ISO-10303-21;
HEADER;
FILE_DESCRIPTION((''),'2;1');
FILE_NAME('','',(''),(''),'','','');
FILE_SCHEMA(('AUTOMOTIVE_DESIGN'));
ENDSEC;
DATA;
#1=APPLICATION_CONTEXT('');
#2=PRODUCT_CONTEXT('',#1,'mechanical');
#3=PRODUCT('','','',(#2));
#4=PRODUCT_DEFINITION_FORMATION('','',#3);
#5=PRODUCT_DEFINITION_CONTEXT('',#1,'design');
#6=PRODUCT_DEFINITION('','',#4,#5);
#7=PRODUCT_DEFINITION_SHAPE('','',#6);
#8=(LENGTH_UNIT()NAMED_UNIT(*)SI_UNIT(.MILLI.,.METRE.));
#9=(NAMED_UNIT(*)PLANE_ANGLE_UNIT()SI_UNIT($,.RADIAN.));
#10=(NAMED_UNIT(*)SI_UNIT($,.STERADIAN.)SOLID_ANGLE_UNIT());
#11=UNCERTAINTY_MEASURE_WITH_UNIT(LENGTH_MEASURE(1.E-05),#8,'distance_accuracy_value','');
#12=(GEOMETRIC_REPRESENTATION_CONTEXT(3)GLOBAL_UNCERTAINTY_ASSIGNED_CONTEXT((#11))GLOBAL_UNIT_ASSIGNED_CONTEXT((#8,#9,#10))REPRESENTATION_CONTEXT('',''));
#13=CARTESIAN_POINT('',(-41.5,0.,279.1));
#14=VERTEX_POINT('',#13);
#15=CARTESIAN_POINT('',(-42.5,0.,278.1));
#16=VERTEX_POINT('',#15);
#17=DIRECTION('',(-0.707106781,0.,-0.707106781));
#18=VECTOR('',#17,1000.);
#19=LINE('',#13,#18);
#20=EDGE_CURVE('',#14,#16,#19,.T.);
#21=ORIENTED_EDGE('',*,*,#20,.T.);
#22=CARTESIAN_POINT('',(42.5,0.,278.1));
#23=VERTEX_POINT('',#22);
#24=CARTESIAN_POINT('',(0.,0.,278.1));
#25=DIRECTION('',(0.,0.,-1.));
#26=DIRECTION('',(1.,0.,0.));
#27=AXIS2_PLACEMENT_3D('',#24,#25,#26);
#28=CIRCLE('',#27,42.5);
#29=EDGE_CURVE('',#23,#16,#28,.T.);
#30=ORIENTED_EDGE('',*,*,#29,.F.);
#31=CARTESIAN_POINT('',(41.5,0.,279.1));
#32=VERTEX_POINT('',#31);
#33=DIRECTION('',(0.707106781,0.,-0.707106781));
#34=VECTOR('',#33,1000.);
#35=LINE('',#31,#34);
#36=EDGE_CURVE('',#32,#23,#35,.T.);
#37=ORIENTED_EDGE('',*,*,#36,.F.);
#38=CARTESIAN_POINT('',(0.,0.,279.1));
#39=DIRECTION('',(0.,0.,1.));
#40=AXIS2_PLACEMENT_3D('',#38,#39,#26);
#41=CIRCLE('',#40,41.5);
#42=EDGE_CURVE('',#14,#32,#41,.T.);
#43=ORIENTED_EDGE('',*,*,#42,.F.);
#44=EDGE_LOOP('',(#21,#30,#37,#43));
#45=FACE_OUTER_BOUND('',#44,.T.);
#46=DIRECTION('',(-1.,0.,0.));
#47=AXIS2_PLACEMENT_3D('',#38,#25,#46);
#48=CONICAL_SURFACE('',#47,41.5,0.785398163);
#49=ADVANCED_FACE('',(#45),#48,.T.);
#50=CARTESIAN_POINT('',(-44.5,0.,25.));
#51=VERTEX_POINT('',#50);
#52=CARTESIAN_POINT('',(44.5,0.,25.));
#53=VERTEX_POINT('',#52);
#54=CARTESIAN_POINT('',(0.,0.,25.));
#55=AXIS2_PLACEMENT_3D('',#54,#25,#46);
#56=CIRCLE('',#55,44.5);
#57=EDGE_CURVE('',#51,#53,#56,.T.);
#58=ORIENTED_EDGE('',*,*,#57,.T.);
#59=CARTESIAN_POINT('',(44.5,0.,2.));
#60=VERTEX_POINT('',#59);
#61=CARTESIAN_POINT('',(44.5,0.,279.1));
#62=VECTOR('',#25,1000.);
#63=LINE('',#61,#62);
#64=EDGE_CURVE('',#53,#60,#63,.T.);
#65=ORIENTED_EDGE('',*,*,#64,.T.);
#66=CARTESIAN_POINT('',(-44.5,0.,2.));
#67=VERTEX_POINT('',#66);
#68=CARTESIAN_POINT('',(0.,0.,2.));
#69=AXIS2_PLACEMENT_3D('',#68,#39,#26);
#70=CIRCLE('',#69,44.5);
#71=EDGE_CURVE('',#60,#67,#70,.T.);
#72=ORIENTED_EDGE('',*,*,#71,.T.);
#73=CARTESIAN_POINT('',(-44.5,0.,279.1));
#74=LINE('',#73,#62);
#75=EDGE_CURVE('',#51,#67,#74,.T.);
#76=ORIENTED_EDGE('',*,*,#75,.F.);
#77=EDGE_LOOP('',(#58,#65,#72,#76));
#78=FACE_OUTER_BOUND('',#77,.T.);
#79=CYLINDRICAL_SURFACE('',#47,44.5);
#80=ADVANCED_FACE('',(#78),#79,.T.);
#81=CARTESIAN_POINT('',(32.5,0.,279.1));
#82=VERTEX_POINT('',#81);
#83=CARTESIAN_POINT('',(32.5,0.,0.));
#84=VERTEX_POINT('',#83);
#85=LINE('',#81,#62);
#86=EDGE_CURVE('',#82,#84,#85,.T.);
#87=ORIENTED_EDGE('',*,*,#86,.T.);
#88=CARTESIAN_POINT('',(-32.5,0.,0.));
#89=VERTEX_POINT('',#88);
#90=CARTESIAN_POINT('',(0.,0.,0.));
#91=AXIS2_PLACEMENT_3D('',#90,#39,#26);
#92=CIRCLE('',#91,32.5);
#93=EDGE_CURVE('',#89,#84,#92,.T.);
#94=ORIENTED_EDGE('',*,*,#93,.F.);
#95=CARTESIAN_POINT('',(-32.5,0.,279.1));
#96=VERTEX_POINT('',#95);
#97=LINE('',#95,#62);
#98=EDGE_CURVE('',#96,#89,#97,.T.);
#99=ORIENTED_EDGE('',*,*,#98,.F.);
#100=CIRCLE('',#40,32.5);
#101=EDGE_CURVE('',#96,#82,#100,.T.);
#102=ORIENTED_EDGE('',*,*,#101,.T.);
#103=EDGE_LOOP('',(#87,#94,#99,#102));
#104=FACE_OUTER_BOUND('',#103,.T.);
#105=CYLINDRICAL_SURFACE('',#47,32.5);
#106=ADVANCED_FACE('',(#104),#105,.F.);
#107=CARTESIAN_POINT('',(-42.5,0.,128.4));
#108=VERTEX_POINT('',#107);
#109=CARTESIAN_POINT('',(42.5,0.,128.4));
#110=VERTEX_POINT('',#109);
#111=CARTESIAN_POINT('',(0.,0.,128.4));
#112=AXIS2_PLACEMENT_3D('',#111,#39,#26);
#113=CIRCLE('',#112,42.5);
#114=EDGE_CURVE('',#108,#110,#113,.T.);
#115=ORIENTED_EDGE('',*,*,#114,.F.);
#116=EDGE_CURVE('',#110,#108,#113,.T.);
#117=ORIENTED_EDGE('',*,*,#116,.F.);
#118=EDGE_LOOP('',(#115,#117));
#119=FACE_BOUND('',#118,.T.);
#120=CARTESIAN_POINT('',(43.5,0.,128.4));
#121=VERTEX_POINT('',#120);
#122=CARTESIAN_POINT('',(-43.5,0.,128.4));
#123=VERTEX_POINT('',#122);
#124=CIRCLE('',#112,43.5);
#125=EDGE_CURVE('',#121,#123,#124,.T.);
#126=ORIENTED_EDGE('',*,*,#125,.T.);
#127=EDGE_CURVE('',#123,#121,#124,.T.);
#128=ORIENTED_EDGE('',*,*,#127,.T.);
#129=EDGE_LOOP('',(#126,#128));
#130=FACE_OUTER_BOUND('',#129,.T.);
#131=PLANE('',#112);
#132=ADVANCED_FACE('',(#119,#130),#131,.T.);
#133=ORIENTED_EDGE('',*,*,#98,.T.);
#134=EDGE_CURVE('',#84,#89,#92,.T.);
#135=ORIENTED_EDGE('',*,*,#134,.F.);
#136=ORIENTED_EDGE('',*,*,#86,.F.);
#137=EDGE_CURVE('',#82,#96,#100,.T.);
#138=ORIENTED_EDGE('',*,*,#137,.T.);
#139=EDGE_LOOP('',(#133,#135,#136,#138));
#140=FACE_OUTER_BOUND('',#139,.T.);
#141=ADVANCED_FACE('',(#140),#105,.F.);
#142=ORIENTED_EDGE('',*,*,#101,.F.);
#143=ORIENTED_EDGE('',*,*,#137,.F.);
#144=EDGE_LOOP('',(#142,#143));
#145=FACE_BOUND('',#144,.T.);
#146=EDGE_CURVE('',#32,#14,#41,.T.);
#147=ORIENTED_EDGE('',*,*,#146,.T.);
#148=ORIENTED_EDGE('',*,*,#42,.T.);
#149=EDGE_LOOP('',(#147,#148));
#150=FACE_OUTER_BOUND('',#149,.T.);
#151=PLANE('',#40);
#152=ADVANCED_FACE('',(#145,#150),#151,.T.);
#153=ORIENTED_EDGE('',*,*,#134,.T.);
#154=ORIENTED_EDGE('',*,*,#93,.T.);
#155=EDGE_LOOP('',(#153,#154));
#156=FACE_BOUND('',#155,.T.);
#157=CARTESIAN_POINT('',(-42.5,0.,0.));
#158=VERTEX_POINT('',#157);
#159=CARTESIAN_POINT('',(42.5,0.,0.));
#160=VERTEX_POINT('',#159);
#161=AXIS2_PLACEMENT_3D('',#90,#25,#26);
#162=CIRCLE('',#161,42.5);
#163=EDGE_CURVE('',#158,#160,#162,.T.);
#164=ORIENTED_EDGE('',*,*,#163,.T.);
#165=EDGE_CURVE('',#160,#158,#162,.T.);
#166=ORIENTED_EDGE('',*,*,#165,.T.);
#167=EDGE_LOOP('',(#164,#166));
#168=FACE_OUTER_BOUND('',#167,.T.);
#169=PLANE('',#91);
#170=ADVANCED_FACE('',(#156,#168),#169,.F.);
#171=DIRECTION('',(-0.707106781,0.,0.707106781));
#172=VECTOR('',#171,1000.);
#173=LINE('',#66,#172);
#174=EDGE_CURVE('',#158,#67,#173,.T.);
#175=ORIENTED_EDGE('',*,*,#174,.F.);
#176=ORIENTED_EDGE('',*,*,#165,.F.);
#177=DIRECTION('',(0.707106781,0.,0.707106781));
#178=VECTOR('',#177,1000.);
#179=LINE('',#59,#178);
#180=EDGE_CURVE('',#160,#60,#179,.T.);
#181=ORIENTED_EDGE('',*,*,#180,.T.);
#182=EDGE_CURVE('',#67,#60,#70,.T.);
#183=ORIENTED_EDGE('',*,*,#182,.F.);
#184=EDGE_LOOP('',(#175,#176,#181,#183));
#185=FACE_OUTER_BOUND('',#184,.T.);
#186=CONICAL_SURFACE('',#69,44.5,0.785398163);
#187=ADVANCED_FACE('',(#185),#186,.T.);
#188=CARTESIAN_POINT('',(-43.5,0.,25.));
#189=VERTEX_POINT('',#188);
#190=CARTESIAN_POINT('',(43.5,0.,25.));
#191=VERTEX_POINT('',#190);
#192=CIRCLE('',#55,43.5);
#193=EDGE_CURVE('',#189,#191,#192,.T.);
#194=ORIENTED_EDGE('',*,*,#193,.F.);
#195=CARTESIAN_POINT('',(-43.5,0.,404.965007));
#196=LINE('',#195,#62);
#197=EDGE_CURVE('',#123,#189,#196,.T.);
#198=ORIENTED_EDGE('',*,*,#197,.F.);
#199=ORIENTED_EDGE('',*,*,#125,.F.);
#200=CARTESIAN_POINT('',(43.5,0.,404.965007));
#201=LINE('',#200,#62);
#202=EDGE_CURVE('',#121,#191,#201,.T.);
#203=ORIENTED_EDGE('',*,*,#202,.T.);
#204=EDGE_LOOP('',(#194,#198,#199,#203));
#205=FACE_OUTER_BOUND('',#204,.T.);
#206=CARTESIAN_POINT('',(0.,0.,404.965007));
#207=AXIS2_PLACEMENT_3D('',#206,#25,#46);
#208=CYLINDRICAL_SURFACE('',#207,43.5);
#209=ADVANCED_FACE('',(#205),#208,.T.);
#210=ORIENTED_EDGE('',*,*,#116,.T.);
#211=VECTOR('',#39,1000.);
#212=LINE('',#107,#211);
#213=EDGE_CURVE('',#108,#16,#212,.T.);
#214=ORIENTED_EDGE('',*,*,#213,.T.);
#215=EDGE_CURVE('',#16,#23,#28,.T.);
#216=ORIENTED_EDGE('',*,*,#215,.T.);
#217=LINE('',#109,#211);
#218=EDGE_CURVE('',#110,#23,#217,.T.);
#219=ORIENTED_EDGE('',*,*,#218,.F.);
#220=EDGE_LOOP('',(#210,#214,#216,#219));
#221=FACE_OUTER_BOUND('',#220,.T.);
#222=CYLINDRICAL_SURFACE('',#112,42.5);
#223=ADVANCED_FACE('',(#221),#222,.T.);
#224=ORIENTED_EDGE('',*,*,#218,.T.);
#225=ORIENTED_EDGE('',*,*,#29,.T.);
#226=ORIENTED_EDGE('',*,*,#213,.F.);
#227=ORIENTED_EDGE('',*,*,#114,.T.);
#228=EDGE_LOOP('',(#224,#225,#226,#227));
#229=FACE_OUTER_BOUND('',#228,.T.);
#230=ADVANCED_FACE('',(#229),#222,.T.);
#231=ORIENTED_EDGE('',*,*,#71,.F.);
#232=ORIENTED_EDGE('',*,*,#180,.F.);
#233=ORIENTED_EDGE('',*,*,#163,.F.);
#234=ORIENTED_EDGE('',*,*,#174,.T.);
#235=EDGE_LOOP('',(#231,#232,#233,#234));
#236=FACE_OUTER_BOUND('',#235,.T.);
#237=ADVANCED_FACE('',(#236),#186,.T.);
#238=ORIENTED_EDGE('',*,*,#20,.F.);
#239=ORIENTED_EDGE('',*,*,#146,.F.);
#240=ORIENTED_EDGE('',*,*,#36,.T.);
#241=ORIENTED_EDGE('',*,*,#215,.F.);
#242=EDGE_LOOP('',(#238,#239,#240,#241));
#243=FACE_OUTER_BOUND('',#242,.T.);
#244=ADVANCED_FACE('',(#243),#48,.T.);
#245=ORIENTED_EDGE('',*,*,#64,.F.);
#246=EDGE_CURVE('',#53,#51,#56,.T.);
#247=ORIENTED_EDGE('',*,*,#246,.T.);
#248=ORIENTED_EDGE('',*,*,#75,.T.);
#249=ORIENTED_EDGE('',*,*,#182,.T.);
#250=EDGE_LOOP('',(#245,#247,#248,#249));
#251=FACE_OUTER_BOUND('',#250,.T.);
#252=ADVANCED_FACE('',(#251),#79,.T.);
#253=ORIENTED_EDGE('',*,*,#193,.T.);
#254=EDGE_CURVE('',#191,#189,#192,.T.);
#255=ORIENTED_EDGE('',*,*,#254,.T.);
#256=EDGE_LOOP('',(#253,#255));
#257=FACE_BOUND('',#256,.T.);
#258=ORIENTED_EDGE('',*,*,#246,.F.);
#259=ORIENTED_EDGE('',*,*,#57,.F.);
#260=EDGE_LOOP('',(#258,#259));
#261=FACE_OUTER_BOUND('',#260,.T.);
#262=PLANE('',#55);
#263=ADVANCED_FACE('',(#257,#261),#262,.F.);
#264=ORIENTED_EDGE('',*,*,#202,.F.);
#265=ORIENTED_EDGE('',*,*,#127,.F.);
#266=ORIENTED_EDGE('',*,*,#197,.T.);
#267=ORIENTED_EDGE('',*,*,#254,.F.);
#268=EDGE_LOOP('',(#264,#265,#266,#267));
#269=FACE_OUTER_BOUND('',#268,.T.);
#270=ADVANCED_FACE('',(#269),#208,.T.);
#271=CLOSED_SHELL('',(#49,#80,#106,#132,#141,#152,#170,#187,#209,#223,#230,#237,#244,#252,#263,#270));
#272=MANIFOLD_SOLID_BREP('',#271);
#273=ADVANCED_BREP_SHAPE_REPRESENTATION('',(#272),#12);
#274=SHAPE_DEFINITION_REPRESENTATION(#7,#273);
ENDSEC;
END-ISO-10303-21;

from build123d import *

# Parameters (mm, degrees)
SKETCH_1_R          = 44.5
SKETCH_1_R_2        = 32.5
EXTRUDE_1_DEPTH     = 279.1
SKETCH_2_R          = 44.5
SKETCH_2_R_2        = 43.5
CUT_EXTRUDE_1_DEPTH = 254.1
CUT_EXTRUDE_START   = -150.7
SKETCH_3_R          = 43.5
SKETCH_3_R_2        = 42.5
CUT_EXTRUDE_2_DEPTH = 150.7
CHAMFER_1_SIZE      = 2
CHAMFER_2_SIZE      = 1


with BuildPart() as part:
    # 草图1 → 凸台-拉伸1 (new body)
    with BuildSketch(Plane.XY):
        Circle(SKETCH_1_R)
        Circle(SKETCH_1_R_2, mode=Mode.SUBTRACT)
    extrude(amount=EXTRUDE_1_DEPTH)

    # 草图2 → 切除-拉伸1 (cut)
    with BuildSketch(Plane(origin=(0, 0, 25), x_dir=(-1, 0, 0), z_dir=(0, 0, -1))):
        Circle(SKETCH_2_R)
        Circle(SKETCH_2_R_2, mode=Mode.SUBTRACT)
    extrude(amount=-CUT_EXTRUDE_1_DEPTH, mode=Mode.SUBTRACT)

    # 草图3 → 切除-拉伸2 (cut)
    with BuildSketch(Plane.XY.offset(279.1).offset(CUT_EXTRUDE_START)):
        with Locations(Location((0, 0, 0), (0, 0, 180))):
            Circle(SKETCH_3_R)
        Circle(SKETCH_3_R_2, mode=Mode.SUBTRACT)
    extrude(amount=CUT_EXTRUDE_2_DEPTH, mode=Mode.SUBTRACT)

    # 倒角1
    chamfer_1_edges = [part.edges().sort_by_distance(p)[0] for p in [
        (-44.5, 0, 0),
    ]]
    chamfer(chamfer_1_edges, length=CHAMFER_1_SIZE)

    # 倒角2
    chamfer_2_edges = [part.edges().sort_by_distance(p)[0] for p in [
        (-42.5, 0, 279.1),
    ]]
    chamfer(chamfer_2_edges, length=CHAMFER_2_SIZE)


solid = part.part
